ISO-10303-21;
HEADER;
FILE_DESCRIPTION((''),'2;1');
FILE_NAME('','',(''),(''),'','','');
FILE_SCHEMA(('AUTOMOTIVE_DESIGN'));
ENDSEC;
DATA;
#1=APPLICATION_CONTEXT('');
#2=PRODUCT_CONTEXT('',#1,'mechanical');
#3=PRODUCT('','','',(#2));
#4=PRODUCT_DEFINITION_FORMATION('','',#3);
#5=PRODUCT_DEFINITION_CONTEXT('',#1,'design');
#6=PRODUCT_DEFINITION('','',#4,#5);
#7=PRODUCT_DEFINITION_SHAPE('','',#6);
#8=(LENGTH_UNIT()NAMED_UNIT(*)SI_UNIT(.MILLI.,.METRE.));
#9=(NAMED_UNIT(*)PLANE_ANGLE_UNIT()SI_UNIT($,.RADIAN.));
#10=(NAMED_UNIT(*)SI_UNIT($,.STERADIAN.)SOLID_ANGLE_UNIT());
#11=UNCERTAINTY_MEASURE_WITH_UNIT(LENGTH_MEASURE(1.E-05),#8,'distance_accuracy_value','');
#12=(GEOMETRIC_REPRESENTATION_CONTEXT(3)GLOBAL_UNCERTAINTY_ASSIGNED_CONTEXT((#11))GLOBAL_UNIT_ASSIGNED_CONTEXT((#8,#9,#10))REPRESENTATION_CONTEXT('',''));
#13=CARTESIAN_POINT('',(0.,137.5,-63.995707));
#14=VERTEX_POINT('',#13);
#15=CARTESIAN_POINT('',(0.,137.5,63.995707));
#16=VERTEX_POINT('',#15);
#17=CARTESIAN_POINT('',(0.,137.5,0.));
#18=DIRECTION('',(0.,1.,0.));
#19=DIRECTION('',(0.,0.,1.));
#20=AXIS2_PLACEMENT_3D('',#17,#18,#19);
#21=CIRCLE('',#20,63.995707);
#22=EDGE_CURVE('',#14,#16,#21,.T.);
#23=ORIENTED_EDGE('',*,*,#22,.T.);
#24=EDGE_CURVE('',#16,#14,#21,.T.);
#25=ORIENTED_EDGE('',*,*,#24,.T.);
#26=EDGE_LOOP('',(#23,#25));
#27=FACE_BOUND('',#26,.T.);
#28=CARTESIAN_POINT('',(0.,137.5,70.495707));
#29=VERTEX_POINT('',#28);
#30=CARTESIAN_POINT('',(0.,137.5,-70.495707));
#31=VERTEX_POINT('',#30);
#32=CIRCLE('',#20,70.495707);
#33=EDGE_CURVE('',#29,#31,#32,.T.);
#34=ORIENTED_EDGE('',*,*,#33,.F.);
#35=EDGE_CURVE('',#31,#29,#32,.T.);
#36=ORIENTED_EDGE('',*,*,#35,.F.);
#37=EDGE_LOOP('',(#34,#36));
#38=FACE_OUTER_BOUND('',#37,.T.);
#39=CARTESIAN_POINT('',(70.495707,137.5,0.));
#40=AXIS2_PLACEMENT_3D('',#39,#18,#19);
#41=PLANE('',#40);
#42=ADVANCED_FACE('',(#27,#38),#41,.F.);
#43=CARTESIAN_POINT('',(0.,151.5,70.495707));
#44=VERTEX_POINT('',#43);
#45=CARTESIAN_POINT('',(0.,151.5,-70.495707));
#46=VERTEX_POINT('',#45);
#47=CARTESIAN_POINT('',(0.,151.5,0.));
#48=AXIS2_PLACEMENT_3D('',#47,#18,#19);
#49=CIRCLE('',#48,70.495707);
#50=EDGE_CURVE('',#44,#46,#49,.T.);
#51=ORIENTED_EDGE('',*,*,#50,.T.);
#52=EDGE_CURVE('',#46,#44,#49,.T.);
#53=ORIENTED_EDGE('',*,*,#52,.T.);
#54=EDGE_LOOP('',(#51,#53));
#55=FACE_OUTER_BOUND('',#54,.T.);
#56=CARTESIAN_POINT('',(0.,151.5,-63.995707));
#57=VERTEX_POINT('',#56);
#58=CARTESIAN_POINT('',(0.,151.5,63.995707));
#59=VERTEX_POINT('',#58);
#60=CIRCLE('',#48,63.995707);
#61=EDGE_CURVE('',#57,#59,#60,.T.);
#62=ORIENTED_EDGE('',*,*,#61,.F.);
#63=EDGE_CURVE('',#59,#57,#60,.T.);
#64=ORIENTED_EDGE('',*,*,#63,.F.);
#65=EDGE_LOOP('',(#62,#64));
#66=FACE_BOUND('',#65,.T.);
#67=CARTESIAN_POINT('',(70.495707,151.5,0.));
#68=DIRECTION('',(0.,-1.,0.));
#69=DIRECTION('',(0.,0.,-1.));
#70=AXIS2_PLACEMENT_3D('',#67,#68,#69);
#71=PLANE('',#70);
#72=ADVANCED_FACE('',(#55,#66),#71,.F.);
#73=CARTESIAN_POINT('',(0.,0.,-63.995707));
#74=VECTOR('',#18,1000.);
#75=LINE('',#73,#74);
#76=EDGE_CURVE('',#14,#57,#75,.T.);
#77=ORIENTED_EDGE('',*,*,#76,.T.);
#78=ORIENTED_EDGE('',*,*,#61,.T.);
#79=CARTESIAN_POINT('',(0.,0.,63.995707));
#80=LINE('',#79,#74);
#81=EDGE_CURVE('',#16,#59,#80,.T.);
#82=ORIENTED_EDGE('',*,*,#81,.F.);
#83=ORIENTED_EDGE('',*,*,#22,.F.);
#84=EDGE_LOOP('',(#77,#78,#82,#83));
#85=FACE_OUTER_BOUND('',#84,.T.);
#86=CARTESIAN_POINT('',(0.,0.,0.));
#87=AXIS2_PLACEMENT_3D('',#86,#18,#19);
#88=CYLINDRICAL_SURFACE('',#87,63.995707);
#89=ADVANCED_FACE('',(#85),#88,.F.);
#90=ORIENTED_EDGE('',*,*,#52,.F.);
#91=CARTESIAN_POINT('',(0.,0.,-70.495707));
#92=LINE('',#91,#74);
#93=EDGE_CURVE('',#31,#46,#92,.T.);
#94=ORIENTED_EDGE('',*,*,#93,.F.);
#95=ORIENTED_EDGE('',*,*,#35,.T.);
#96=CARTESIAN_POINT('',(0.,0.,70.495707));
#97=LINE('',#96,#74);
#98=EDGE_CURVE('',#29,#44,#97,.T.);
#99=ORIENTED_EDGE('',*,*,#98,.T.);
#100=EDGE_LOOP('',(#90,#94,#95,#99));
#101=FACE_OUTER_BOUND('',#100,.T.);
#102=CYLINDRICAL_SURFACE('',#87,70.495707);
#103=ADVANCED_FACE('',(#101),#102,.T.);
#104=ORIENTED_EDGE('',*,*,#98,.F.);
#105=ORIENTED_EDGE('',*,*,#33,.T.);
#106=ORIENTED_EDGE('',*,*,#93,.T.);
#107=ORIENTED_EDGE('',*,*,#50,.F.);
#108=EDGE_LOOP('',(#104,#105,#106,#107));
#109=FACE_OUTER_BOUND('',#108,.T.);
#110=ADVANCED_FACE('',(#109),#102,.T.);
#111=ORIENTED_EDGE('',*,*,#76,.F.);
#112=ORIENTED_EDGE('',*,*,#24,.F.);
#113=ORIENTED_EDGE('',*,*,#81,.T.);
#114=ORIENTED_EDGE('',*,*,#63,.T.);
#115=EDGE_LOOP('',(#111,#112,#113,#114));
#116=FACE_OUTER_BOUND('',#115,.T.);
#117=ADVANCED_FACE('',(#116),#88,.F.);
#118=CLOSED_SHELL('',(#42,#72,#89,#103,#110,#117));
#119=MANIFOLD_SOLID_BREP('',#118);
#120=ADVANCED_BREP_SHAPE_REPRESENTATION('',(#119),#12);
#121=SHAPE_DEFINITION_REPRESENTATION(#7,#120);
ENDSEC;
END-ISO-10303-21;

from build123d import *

# Parameters (mm, degrees)
SKETCH1_W = 6.5
SKETCH1_H = 14


with BuildPart() as part:
    # Sketch1 → Revolve1 (revolve)
    with BuildSketch(Plane.XY, mode=Mode.PRIVATE) as revolve1_sk:
        with Locations((67.245706961, 144.5)):
            Rectangle(SKETCH1_W, SKETCH1_H)
    revolve(revolve1_sk.sketch.rotate(Axis((0, 0, 0), (0, -1, 0)), 90), axis=Axis((0, 0, 0), (0, -1, 0)))


solid = part.part
